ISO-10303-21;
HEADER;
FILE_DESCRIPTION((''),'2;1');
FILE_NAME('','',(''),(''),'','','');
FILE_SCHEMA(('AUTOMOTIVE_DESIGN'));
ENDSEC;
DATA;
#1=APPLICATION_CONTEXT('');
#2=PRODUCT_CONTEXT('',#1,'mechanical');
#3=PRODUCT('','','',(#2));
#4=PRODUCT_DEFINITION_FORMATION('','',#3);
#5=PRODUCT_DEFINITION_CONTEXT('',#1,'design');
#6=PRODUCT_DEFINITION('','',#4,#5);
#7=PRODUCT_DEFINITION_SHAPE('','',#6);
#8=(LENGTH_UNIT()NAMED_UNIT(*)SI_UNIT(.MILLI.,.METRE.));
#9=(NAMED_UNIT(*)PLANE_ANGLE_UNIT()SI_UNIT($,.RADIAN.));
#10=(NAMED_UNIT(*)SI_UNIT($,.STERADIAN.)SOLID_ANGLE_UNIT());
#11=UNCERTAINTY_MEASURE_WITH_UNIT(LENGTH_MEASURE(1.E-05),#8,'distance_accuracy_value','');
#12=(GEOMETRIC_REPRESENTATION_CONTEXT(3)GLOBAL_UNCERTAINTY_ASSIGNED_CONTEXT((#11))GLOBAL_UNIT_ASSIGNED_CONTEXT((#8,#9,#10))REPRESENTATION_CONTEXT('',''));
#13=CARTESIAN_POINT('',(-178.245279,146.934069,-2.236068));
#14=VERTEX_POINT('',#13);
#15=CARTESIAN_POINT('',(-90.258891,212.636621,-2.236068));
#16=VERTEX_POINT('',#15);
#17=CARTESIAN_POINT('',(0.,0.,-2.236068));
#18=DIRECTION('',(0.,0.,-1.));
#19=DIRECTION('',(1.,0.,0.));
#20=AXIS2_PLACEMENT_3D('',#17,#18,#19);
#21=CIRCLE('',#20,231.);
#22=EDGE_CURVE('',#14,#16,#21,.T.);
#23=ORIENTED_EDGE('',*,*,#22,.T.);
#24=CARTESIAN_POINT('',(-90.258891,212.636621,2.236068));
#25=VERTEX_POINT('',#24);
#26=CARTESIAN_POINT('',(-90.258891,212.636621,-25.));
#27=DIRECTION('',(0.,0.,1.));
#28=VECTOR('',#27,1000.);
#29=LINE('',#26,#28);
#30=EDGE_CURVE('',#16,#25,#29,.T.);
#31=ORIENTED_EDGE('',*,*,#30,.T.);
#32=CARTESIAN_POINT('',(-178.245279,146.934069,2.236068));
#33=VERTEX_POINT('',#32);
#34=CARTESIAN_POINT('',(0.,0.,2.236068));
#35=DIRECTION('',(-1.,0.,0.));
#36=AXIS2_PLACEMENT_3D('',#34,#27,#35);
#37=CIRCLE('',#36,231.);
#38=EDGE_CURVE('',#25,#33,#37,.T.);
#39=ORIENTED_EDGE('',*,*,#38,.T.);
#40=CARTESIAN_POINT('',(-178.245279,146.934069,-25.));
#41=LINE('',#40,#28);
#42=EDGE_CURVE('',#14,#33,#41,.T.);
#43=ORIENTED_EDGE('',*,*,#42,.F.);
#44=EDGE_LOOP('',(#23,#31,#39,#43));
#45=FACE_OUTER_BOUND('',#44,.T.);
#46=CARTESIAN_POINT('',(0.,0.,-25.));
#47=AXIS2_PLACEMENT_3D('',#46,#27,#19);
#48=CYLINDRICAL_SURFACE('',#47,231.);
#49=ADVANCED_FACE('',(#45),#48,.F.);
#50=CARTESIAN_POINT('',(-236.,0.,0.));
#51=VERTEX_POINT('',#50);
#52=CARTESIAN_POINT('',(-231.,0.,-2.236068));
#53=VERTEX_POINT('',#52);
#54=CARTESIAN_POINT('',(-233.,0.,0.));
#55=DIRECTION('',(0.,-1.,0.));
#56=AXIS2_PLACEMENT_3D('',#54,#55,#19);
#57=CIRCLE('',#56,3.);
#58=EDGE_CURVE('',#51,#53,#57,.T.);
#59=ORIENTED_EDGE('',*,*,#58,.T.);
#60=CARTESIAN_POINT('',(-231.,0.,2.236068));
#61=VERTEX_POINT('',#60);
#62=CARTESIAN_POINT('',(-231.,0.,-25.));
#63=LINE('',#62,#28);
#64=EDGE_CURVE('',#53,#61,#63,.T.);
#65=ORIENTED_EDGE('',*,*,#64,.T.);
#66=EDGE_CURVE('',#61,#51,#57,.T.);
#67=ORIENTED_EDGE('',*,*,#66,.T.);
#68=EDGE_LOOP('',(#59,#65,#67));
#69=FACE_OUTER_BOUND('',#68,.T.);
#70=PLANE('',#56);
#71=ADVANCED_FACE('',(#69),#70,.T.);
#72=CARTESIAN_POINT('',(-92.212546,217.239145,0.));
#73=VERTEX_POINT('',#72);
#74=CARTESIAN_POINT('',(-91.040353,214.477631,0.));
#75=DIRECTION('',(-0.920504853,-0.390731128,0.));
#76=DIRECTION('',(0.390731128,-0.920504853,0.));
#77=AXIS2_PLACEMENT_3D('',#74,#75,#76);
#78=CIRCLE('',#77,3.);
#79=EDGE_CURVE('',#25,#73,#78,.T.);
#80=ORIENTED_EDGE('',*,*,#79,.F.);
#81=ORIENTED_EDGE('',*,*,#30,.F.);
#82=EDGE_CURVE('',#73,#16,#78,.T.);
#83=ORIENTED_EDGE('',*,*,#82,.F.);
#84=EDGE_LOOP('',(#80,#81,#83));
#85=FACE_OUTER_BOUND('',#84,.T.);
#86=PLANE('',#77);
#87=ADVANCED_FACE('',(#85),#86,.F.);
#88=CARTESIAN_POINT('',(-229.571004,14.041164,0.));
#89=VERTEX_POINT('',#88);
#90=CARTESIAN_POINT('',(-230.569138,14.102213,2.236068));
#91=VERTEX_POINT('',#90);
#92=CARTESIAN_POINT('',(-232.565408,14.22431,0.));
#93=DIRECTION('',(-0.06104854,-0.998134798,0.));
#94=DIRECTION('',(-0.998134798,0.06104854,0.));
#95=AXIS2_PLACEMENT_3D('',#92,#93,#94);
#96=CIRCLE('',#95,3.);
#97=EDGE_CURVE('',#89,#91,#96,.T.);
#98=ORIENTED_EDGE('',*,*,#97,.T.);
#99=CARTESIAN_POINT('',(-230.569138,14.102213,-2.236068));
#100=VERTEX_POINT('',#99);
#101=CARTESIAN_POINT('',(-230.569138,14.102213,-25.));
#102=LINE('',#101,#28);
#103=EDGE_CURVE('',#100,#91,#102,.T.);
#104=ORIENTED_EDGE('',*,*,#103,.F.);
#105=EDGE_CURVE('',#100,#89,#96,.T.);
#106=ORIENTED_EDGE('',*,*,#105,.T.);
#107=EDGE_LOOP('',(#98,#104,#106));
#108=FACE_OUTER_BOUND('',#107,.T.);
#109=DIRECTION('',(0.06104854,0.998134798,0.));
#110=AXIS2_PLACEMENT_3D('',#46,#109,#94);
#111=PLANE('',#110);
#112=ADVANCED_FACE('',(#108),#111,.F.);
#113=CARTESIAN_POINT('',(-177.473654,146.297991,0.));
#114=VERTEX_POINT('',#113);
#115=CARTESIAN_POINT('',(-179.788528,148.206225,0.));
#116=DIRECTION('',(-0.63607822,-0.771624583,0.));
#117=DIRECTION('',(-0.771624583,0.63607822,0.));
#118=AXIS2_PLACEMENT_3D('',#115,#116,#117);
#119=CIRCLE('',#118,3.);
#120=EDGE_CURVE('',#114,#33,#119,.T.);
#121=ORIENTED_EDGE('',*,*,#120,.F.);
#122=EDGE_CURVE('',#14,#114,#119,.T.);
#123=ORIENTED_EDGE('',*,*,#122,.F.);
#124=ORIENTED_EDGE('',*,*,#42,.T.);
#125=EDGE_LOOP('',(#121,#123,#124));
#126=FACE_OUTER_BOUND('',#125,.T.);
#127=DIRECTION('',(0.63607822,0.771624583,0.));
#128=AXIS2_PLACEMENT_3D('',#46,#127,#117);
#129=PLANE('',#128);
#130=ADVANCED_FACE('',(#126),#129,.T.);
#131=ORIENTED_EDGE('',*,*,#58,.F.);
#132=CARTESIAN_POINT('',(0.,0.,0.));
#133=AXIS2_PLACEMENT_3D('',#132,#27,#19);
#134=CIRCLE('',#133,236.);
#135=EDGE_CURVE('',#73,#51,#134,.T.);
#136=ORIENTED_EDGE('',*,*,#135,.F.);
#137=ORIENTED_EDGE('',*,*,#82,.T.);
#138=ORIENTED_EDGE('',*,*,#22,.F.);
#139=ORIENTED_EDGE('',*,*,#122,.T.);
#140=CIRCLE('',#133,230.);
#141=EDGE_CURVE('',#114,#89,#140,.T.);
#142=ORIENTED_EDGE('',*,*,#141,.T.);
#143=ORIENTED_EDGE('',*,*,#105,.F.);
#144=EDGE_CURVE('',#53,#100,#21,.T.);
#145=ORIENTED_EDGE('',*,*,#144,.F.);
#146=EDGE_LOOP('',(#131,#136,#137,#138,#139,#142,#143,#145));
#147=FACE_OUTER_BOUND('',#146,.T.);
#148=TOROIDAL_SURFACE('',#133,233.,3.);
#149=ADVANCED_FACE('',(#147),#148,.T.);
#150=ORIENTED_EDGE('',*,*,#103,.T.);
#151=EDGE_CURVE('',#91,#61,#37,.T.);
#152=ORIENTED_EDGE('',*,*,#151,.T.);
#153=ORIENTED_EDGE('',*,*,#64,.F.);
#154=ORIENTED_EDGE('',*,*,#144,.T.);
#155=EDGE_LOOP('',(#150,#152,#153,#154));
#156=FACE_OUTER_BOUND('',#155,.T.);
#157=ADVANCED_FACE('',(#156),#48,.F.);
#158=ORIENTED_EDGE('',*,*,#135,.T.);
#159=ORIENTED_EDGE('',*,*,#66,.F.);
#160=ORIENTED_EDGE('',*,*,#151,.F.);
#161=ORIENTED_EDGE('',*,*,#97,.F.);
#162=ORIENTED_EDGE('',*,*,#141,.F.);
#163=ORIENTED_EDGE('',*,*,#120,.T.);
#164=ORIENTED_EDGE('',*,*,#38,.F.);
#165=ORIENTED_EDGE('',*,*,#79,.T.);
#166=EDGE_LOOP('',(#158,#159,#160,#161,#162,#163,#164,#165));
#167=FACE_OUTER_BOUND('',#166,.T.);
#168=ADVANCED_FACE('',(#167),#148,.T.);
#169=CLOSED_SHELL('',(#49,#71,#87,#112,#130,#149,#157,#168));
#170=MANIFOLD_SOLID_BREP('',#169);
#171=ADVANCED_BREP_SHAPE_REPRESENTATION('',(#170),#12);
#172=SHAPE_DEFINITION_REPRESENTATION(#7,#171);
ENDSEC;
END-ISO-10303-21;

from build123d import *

# Parameters (mm, degrees)
SWEEP1_PROFILE_R   = 3
CUT_EXTRUDE1_DEPTH = 25


with BuildPart() as part:
    # Sweep1: sweep along a path in Sketch1
    with BuildLine(Plane.XY) as sweep1_path:
        ThreePointArc((-91.040352938, 214.477630854), (-194.295396542, 128.601317578), (-233, 0))
    # Sweep1 profile (on start of the path) → Sweep1 (sweep)
    with BuildSketch(Plane(origin=(-91.040352938, 214.477630854, 0), x_dir=(0.39073112848927155, -0.9205048534524413, 0), z_dir=(-0.9205048534524413, -0.39073112848927155, 0))):
        Circle(SWEEP1_PROFILE_R)
    sweep(path=sweep1_path.line)

    # Sketch6 → Cut-Extrude1 (cut, symmetric)
    with BuildSketch(Plane.XY):
        with BuildLine():
            Line((0, 0), (-230.569138435, 14.102212633))
            ThreePointArc((-230.569138435, 14.102212633), (-230.892259483, 7.054396551), (-231, 0))
            Line((-231, 0), (0, 0))
        make_face()
        with BuildLine():
            Line((0, 0), (-90.258890681, 212.636621148))
            ThreePointArc((-90.258890681, 212.636621148), (-138.212982732, 185.089630732), (-178.245278763, 146.934068884))
            Line((-178.245278763, 146.934068884), (0, 0))
        make_face()
    extrude(amount=CUT_EXTRUDE1_DEPTH, both=True, mode=Mode.SUBTRACT)


solid = part.part
